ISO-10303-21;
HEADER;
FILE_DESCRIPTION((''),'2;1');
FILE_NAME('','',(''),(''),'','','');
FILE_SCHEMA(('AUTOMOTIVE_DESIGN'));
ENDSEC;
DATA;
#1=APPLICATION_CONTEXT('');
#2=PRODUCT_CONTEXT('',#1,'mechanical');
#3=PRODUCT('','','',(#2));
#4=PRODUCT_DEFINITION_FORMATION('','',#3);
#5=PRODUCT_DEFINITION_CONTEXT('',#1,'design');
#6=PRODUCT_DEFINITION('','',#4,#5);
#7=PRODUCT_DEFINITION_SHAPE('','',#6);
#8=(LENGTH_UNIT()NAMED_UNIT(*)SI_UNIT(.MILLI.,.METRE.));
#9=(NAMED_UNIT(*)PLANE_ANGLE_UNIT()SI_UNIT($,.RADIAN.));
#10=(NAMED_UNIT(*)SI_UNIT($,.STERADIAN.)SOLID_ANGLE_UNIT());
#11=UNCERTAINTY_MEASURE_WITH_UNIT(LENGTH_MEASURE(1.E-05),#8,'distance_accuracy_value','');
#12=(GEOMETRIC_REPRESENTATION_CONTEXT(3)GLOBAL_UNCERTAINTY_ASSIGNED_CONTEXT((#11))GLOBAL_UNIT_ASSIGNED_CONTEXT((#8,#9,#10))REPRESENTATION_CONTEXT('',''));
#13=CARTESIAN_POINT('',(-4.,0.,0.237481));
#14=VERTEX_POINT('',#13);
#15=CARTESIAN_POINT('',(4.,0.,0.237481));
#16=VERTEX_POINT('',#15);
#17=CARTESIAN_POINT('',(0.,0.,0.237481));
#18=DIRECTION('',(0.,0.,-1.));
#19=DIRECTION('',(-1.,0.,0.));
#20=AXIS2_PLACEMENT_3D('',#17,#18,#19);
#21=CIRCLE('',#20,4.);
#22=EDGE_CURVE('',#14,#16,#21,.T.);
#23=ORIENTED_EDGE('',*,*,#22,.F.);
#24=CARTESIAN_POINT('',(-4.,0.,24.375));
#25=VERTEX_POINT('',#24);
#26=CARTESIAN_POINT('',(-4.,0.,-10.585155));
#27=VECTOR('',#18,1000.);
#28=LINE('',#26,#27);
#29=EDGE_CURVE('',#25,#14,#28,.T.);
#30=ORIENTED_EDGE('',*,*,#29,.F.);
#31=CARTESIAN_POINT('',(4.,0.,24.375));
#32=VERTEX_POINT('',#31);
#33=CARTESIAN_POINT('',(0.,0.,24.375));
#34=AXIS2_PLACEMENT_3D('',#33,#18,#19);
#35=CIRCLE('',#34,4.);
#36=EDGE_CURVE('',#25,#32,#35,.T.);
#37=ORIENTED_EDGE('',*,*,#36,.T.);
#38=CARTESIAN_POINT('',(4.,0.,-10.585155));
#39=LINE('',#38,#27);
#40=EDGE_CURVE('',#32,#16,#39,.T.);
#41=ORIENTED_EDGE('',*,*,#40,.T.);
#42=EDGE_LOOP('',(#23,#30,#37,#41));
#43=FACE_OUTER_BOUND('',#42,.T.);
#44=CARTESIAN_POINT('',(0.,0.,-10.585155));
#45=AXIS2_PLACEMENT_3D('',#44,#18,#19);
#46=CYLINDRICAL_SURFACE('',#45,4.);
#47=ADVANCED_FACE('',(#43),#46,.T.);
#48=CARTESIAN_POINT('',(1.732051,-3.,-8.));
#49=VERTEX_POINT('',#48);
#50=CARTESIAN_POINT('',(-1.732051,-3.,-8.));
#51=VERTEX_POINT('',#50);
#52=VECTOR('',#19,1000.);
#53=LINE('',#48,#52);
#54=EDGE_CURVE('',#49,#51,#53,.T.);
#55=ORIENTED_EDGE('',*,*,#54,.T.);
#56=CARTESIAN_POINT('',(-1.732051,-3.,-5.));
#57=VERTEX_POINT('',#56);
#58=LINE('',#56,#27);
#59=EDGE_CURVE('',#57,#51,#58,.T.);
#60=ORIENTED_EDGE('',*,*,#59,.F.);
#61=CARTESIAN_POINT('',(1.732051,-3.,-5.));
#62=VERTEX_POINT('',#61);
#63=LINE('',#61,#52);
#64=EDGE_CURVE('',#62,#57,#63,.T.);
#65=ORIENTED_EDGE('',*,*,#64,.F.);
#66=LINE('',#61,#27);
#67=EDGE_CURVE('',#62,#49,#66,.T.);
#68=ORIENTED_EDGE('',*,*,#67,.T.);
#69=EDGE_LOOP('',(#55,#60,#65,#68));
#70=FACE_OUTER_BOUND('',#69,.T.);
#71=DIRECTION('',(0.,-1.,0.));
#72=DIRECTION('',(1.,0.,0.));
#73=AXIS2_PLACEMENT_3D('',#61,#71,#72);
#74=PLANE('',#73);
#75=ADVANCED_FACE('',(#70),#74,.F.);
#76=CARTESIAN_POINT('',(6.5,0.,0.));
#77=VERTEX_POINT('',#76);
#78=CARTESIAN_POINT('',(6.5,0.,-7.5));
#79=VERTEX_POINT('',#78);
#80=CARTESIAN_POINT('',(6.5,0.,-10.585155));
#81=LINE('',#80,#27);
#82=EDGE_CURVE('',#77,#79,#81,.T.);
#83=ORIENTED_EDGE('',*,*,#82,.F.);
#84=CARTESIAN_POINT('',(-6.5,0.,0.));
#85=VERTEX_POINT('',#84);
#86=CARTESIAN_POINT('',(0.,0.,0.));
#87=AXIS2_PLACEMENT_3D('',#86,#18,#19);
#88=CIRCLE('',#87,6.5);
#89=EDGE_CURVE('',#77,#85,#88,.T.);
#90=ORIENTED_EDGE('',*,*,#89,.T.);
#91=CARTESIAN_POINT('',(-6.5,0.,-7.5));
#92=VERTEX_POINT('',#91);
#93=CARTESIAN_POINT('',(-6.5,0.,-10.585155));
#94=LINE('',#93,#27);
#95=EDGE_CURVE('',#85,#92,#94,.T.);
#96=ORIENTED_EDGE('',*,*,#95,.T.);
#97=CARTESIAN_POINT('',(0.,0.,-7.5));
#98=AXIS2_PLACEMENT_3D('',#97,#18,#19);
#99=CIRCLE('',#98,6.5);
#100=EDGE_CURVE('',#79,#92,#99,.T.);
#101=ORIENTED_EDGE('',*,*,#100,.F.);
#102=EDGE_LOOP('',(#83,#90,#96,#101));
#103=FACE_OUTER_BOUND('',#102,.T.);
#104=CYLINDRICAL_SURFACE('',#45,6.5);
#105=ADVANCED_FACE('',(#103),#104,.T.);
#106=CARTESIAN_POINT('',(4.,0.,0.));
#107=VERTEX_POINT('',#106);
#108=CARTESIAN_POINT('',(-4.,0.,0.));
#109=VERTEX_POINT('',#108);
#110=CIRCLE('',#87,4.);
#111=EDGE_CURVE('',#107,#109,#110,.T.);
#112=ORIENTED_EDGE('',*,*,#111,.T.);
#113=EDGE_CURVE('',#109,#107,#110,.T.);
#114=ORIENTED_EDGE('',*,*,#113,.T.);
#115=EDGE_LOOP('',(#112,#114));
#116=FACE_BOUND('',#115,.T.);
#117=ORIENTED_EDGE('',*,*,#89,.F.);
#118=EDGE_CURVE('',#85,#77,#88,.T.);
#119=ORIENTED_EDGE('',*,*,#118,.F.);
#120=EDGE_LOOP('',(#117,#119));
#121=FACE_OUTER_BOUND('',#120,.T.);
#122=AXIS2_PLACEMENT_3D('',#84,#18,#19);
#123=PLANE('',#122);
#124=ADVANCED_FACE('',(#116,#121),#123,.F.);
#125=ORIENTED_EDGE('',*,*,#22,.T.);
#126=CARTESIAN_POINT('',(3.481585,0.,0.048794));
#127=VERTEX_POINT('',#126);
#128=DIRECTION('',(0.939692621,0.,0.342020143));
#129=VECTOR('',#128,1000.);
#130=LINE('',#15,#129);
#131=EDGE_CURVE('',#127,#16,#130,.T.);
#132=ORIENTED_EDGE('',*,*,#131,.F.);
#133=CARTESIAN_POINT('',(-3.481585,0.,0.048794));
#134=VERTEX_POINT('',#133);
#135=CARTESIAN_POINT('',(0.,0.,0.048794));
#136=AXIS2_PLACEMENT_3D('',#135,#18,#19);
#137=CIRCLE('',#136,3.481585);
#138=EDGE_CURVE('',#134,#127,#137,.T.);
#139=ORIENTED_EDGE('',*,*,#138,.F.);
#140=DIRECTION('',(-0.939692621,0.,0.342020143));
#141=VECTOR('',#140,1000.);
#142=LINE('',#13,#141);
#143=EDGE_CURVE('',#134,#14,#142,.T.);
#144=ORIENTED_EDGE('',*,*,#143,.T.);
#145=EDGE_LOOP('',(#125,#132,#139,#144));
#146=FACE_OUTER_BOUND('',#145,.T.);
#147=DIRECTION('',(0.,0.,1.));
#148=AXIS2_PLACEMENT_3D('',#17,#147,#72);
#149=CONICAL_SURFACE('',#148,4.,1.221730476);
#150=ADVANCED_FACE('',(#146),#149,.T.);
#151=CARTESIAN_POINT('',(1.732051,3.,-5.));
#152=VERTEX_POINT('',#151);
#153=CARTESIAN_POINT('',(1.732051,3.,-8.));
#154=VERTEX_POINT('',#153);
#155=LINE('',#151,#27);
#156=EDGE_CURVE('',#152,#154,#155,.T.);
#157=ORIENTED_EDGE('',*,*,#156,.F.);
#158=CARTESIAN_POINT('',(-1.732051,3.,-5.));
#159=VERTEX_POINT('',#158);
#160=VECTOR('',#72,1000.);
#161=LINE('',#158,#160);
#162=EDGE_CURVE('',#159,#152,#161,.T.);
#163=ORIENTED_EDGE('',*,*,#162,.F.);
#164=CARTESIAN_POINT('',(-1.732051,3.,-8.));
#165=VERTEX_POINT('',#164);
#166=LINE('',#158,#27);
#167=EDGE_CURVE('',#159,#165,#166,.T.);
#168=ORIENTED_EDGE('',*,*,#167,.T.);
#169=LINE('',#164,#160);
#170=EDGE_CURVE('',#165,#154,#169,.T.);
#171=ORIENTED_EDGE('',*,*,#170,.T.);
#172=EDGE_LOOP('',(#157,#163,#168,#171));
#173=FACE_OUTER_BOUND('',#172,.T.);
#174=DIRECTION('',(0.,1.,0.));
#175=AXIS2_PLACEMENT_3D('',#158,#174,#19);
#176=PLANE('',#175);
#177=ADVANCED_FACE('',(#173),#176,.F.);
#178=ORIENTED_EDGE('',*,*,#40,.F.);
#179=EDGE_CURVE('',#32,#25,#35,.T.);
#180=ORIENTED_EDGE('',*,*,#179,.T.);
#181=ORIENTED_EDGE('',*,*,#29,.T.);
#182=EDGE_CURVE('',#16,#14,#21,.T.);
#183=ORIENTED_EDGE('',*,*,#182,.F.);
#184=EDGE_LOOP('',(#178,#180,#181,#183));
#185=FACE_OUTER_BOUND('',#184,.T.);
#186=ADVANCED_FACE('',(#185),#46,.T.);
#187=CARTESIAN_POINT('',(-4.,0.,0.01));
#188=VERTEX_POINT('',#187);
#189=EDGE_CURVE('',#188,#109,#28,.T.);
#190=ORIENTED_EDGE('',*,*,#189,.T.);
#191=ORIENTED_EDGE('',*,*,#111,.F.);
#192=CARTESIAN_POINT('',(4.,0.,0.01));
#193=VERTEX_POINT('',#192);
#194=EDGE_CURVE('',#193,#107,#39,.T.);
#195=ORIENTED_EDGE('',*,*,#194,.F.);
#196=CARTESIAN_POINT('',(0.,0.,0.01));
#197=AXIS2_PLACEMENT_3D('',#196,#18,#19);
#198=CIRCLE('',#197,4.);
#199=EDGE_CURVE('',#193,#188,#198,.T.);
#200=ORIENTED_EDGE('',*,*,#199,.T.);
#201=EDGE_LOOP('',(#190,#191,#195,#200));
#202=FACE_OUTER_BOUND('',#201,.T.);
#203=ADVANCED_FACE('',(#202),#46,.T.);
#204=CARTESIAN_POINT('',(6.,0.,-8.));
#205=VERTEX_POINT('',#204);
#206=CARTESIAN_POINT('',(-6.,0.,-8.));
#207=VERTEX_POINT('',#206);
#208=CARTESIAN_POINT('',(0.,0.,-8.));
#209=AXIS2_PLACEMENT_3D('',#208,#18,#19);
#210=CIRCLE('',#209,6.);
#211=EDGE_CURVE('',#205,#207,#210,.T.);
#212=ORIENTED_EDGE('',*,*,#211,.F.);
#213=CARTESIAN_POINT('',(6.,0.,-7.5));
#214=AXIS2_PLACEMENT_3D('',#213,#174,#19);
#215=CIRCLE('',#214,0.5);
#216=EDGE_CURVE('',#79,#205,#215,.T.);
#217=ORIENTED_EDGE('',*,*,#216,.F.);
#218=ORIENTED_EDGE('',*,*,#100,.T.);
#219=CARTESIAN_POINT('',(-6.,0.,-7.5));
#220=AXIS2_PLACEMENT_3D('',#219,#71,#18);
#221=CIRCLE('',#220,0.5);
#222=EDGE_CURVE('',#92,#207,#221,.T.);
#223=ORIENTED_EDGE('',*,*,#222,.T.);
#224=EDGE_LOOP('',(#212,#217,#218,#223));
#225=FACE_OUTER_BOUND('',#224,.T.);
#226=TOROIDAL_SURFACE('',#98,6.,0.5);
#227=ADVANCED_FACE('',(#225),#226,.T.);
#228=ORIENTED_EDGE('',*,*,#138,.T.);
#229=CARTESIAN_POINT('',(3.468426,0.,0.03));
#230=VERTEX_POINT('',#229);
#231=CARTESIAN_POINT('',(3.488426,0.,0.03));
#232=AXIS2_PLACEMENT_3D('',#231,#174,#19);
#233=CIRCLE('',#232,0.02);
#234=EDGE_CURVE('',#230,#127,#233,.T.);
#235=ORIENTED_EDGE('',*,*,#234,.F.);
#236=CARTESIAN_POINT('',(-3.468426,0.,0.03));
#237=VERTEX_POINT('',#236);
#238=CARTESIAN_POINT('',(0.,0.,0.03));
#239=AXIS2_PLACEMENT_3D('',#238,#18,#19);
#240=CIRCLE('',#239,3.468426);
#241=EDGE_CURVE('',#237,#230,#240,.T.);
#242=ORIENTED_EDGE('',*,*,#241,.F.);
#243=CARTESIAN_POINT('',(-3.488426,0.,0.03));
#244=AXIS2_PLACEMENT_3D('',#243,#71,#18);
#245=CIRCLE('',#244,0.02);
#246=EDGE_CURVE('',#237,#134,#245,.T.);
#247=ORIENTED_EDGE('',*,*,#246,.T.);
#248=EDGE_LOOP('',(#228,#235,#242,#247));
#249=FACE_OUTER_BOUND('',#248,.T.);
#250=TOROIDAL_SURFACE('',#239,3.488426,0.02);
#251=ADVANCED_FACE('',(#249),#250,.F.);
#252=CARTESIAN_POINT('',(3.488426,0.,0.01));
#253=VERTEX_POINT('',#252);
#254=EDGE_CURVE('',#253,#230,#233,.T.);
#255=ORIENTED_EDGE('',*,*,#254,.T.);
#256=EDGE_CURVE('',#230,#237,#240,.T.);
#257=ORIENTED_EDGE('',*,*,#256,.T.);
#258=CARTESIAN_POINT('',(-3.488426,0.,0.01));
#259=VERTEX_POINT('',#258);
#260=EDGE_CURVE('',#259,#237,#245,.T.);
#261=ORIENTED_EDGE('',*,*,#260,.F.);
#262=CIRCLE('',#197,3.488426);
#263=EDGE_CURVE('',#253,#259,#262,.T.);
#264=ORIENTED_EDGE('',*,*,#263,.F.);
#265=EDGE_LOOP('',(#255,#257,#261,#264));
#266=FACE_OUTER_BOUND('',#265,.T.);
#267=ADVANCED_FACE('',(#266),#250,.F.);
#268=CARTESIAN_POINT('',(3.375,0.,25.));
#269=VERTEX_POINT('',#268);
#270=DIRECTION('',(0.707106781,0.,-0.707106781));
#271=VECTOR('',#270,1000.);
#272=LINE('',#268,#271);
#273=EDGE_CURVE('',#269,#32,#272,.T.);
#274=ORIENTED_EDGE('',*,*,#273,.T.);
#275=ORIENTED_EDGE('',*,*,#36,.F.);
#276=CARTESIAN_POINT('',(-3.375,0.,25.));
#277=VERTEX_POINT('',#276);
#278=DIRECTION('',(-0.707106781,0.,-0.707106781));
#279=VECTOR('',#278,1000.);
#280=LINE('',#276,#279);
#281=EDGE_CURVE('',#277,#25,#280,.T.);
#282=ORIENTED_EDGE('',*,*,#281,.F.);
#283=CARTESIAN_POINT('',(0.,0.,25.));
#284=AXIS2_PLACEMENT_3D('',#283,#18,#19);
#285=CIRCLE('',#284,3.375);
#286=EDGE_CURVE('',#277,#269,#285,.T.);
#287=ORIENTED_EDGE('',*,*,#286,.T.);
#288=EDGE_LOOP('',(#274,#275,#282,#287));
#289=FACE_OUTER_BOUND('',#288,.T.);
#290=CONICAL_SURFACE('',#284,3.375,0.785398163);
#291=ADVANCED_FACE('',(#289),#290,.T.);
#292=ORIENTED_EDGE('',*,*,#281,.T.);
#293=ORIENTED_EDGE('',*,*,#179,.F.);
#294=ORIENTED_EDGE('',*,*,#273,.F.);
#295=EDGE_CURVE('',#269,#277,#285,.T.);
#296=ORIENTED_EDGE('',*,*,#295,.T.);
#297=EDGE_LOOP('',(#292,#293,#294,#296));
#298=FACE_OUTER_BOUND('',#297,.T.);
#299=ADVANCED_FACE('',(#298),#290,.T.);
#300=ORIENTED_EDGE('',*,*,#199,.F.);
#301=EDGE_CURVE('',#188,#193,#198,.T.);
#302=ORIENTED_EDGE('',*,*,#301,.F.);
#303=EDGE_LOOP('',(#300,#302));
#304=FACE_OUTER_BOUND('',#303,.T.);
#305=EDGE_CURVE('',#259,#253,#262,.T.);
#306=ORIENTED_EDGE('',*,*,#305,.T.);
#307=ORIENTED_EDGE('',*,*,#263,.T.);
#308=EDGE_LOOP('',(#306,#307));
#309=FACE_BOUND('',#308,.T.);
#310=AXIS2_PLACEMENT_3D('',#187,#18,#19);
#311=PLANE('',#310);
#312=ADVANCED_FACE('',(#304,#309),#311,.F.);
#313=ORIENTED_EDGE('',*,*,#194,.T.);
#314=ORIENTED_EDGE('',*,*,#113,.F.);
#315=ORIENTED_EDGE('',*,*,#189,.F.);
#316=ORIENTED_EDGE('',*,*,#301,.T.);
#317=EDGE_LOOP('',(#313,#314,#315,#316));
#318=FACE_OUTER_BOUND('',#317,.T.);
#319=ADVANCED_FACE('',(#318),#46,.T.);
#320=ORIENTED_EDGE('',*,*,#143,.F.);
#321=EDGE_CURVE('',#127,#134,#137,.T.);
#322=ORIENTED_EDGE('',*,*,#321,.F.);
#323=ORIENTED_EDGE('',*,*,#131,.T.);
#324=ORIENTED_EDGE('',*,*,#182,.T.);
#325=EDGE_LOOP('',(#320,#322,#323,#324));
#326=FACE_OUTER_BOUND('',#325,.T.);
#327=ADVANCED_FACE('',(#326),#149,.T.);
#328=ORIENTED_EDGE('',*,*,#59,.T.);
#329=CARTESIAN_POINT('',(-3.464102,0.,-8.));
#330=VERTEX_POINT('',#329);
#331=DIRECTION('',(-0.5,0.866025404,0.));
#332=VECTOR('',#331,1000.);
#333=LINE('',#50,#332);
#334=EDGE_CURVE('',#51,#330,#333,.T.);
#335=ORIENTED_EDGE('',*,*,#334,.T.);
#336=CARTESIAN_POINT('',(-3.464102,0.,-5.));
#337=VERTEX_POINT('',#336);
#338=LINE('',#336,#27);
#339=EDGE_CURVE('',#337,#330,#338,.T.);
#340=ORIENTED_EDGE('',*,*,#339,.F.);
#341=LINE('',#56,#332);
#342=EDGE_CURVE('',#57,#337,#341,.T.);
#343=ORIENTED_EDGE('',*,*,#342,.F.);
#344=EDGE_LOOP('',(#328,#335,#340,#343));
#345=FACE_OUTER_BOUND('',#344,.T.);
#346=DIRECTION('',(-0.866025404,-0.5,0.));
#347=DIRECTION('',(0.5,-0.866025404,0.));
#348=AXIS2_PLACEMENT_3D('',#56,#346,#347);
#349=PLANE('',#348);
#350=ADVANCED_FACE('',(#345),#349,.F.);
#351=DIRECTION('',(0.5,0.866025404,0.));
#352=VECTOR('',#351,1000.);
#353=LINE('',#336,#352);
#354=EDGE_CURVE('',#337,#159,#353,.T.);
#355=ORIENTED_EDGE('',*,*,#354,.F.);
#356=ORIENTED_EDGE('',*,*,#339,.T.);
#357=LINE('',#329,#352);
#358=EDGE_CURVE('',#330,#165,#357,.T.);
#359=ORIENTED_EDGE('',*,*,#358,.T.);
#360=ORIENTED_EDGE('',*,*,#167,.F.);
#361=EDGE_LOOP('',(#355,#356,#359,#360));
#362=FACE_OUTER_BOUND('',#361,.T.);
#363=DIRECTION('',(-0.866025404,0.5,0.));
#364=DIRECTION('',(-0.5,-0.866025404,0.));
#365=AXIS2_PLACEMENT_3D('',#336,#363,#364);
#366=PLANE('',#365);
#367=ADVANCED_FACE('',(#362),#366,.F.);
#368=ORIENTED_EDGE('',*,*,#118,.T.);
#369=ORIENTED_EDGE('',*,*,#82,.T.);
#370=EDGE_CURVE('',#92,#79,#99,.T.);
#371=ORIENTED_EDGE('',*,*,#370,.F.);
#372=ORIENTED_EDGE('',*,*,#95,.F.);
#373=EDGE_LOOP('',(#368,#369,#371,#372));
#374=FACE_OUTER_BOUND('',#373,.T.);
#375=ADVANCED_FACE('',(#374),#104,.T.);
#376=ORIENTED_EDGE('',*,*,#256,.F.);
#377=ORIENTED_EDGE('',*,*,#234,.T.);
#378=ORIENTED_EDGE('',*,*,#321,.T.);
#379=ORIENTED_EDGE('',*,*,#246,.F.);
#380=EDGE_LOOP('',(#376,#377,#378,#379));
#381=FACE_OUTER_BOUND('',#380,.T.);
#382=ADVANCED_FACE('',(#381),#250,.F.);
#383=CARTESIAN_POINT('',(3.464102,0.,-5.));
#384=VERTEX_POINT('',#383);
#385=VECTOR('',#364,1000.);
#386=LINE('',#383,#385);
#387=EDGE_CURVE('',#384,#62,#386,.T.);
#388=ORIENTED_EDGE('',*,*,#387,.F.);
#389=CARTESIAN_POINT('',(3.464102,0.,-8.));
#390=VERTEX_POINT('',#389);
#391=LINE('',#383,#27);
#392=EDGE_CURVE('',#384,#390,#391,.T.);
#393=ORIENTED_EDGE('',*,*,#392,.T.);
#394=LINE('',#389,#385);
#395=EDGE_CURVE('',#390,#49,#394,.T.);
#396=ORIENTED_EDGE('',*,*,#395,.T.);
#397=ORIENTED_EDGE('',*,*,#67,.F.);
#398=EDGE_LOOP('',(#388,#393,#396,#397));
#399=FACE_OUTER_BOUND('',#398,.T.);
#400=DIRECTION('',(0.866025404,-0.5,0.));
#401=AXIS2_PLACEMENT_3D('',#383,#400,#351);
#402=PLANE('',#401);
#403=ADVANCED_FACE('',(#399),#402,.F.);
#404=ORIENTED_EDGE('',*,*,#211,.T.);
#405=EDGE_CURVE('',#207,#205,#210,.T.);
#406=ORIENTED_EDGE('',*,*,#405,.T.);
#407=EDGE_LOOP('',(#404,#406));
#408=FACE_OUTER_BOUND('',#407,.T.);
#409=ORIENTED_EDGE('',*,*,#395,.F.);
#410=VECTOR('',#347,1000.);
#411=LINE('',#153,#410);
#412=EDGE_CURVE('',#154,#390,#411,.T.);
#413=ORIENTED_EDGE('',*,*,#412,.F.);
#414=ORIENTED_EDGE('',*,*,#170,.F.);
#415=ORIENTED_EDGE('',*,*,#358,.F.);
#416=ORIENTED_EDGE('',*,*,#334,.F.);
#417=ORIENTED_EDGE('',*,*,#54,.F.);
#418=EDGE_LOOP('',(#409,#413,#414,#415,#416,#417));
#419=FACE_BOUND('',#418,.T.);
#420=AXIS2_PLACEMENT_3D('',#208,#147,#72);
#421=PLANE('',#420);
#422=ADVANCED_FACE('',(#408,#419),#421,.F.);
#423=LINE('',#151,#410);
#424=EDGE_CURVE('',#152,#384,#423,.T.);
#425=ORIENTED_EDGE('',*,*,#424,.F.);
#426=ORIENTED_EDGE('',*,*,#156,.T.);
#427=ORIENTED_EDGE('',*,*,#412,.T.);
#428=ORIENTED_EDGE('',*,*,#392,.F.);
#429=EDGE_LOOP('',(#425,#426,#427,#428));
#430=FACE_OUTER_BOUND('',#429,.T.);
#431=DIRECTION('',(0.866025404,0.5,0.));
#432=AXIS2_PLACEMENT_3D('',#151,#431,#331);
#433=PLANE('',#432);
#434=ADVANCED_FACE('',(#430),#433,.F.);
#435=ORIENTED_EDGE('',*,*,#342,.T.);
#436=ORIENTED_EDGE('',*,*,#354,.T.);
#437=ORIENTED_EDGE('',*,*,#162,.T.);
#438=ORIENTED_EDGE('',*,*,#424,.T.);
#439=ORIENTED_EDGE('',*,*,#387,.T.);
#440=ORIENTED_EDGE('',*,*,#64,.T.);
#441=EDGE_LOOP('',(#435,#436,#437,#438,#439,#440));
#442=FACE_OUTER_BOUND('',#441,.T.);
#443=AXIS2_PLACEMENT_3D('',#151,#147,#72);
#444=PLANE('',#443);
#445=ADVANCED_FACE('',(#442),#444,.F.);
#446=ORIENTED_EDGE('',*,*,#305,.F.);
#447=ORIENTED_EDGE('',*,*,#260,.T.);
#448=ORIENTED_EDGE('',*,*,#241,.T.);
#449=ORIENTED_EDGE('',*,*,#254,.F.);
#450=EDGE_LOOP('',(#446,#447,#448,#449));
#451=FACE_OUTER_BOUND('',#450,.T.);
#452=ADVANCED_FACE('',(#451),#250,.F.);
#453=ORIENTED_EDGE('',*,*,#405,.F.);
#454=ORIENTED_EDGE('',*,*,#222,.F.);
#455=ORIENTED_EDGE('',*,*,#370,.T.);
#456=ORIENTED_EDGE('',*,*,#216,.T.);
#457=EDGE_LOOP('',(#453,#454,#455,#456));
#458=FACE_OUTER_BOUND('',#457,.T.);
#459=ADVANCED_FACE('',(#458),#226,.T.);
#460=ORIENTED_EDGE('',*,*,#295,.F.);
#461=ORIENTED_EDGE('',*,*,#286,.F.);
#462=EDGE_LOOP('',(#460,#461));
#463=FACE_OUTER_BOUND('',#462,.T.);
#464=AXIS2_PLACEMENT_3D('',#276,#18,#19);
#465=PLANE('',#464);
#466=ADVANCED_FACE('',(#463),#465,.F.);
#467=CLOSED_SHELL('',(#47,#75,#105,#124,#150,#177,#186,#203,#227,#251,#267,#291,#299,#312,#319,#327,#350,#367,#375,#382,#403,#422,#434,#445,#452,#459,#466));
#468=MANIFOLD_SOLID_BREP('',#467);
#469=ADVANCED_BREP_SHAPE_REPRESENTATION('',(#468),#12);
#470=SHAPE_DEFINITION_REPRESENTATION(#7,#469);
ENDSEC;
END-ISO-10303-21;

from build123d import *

# Parameters (mm, degrees)
CUT_EXTRUDE1_DEPTH = 3


with BuildPart() as part:
    # Logo3_bib1 → Revolve1 (revolve)
    with BuildSketch(Plane(origin=(0, 0, 0), x_dir=(-1, 0, 0), z_dir=(0, -1, 0))):
        with BuildLine():
            Line((0, -25), (0, 8))
            Line((0, 8), (6, 8))
            ThreePointArc((6, 8), (6.353553391, 7.853553391), (6.5, 7.5))
            Line((6.5, 7.5), (6.5, 0))
            Line((6.5, 0), (4, 0))
            Line((4, 0), (4, -0.01))
            Line((4, -0.01), (3.488425636, -0.01))
            ThreePointArc((3.488425636, -0.01), (3.468729481, -0.026527036), (3.481585234, -0.048793852))
            Line((3.481585234, -0.048793852), (4, -0.237481396))
            Line((4, -0.237481396), (4, -24.375))
            Line((4, -24.375), (3.375, -25))
            Line((3.375, -25), (0, -25))
        make_face()
    revolve(axis=Axis((0, 0, -10.585154653), (0, 0, 1)))

    # Logo3_bib2 → Cut-Extrude1 (cut)
    with BuildSketch(Plane(origin=(0, 0, -8), x_dir=(1, 0, 0), z_dir=(0, 0, -1))):
        Polygon((3.464101615, 0), (1.732050808, 3), (-1.732050808, 3), (-3.464101615, 0), (-1.732050808, -3), (1.732050808, -3), align=None)
    extrude(amount=-CUT_EXTRUDE1_DEPTH, mode=Mode.SUBTRACT)


solid = part.part
